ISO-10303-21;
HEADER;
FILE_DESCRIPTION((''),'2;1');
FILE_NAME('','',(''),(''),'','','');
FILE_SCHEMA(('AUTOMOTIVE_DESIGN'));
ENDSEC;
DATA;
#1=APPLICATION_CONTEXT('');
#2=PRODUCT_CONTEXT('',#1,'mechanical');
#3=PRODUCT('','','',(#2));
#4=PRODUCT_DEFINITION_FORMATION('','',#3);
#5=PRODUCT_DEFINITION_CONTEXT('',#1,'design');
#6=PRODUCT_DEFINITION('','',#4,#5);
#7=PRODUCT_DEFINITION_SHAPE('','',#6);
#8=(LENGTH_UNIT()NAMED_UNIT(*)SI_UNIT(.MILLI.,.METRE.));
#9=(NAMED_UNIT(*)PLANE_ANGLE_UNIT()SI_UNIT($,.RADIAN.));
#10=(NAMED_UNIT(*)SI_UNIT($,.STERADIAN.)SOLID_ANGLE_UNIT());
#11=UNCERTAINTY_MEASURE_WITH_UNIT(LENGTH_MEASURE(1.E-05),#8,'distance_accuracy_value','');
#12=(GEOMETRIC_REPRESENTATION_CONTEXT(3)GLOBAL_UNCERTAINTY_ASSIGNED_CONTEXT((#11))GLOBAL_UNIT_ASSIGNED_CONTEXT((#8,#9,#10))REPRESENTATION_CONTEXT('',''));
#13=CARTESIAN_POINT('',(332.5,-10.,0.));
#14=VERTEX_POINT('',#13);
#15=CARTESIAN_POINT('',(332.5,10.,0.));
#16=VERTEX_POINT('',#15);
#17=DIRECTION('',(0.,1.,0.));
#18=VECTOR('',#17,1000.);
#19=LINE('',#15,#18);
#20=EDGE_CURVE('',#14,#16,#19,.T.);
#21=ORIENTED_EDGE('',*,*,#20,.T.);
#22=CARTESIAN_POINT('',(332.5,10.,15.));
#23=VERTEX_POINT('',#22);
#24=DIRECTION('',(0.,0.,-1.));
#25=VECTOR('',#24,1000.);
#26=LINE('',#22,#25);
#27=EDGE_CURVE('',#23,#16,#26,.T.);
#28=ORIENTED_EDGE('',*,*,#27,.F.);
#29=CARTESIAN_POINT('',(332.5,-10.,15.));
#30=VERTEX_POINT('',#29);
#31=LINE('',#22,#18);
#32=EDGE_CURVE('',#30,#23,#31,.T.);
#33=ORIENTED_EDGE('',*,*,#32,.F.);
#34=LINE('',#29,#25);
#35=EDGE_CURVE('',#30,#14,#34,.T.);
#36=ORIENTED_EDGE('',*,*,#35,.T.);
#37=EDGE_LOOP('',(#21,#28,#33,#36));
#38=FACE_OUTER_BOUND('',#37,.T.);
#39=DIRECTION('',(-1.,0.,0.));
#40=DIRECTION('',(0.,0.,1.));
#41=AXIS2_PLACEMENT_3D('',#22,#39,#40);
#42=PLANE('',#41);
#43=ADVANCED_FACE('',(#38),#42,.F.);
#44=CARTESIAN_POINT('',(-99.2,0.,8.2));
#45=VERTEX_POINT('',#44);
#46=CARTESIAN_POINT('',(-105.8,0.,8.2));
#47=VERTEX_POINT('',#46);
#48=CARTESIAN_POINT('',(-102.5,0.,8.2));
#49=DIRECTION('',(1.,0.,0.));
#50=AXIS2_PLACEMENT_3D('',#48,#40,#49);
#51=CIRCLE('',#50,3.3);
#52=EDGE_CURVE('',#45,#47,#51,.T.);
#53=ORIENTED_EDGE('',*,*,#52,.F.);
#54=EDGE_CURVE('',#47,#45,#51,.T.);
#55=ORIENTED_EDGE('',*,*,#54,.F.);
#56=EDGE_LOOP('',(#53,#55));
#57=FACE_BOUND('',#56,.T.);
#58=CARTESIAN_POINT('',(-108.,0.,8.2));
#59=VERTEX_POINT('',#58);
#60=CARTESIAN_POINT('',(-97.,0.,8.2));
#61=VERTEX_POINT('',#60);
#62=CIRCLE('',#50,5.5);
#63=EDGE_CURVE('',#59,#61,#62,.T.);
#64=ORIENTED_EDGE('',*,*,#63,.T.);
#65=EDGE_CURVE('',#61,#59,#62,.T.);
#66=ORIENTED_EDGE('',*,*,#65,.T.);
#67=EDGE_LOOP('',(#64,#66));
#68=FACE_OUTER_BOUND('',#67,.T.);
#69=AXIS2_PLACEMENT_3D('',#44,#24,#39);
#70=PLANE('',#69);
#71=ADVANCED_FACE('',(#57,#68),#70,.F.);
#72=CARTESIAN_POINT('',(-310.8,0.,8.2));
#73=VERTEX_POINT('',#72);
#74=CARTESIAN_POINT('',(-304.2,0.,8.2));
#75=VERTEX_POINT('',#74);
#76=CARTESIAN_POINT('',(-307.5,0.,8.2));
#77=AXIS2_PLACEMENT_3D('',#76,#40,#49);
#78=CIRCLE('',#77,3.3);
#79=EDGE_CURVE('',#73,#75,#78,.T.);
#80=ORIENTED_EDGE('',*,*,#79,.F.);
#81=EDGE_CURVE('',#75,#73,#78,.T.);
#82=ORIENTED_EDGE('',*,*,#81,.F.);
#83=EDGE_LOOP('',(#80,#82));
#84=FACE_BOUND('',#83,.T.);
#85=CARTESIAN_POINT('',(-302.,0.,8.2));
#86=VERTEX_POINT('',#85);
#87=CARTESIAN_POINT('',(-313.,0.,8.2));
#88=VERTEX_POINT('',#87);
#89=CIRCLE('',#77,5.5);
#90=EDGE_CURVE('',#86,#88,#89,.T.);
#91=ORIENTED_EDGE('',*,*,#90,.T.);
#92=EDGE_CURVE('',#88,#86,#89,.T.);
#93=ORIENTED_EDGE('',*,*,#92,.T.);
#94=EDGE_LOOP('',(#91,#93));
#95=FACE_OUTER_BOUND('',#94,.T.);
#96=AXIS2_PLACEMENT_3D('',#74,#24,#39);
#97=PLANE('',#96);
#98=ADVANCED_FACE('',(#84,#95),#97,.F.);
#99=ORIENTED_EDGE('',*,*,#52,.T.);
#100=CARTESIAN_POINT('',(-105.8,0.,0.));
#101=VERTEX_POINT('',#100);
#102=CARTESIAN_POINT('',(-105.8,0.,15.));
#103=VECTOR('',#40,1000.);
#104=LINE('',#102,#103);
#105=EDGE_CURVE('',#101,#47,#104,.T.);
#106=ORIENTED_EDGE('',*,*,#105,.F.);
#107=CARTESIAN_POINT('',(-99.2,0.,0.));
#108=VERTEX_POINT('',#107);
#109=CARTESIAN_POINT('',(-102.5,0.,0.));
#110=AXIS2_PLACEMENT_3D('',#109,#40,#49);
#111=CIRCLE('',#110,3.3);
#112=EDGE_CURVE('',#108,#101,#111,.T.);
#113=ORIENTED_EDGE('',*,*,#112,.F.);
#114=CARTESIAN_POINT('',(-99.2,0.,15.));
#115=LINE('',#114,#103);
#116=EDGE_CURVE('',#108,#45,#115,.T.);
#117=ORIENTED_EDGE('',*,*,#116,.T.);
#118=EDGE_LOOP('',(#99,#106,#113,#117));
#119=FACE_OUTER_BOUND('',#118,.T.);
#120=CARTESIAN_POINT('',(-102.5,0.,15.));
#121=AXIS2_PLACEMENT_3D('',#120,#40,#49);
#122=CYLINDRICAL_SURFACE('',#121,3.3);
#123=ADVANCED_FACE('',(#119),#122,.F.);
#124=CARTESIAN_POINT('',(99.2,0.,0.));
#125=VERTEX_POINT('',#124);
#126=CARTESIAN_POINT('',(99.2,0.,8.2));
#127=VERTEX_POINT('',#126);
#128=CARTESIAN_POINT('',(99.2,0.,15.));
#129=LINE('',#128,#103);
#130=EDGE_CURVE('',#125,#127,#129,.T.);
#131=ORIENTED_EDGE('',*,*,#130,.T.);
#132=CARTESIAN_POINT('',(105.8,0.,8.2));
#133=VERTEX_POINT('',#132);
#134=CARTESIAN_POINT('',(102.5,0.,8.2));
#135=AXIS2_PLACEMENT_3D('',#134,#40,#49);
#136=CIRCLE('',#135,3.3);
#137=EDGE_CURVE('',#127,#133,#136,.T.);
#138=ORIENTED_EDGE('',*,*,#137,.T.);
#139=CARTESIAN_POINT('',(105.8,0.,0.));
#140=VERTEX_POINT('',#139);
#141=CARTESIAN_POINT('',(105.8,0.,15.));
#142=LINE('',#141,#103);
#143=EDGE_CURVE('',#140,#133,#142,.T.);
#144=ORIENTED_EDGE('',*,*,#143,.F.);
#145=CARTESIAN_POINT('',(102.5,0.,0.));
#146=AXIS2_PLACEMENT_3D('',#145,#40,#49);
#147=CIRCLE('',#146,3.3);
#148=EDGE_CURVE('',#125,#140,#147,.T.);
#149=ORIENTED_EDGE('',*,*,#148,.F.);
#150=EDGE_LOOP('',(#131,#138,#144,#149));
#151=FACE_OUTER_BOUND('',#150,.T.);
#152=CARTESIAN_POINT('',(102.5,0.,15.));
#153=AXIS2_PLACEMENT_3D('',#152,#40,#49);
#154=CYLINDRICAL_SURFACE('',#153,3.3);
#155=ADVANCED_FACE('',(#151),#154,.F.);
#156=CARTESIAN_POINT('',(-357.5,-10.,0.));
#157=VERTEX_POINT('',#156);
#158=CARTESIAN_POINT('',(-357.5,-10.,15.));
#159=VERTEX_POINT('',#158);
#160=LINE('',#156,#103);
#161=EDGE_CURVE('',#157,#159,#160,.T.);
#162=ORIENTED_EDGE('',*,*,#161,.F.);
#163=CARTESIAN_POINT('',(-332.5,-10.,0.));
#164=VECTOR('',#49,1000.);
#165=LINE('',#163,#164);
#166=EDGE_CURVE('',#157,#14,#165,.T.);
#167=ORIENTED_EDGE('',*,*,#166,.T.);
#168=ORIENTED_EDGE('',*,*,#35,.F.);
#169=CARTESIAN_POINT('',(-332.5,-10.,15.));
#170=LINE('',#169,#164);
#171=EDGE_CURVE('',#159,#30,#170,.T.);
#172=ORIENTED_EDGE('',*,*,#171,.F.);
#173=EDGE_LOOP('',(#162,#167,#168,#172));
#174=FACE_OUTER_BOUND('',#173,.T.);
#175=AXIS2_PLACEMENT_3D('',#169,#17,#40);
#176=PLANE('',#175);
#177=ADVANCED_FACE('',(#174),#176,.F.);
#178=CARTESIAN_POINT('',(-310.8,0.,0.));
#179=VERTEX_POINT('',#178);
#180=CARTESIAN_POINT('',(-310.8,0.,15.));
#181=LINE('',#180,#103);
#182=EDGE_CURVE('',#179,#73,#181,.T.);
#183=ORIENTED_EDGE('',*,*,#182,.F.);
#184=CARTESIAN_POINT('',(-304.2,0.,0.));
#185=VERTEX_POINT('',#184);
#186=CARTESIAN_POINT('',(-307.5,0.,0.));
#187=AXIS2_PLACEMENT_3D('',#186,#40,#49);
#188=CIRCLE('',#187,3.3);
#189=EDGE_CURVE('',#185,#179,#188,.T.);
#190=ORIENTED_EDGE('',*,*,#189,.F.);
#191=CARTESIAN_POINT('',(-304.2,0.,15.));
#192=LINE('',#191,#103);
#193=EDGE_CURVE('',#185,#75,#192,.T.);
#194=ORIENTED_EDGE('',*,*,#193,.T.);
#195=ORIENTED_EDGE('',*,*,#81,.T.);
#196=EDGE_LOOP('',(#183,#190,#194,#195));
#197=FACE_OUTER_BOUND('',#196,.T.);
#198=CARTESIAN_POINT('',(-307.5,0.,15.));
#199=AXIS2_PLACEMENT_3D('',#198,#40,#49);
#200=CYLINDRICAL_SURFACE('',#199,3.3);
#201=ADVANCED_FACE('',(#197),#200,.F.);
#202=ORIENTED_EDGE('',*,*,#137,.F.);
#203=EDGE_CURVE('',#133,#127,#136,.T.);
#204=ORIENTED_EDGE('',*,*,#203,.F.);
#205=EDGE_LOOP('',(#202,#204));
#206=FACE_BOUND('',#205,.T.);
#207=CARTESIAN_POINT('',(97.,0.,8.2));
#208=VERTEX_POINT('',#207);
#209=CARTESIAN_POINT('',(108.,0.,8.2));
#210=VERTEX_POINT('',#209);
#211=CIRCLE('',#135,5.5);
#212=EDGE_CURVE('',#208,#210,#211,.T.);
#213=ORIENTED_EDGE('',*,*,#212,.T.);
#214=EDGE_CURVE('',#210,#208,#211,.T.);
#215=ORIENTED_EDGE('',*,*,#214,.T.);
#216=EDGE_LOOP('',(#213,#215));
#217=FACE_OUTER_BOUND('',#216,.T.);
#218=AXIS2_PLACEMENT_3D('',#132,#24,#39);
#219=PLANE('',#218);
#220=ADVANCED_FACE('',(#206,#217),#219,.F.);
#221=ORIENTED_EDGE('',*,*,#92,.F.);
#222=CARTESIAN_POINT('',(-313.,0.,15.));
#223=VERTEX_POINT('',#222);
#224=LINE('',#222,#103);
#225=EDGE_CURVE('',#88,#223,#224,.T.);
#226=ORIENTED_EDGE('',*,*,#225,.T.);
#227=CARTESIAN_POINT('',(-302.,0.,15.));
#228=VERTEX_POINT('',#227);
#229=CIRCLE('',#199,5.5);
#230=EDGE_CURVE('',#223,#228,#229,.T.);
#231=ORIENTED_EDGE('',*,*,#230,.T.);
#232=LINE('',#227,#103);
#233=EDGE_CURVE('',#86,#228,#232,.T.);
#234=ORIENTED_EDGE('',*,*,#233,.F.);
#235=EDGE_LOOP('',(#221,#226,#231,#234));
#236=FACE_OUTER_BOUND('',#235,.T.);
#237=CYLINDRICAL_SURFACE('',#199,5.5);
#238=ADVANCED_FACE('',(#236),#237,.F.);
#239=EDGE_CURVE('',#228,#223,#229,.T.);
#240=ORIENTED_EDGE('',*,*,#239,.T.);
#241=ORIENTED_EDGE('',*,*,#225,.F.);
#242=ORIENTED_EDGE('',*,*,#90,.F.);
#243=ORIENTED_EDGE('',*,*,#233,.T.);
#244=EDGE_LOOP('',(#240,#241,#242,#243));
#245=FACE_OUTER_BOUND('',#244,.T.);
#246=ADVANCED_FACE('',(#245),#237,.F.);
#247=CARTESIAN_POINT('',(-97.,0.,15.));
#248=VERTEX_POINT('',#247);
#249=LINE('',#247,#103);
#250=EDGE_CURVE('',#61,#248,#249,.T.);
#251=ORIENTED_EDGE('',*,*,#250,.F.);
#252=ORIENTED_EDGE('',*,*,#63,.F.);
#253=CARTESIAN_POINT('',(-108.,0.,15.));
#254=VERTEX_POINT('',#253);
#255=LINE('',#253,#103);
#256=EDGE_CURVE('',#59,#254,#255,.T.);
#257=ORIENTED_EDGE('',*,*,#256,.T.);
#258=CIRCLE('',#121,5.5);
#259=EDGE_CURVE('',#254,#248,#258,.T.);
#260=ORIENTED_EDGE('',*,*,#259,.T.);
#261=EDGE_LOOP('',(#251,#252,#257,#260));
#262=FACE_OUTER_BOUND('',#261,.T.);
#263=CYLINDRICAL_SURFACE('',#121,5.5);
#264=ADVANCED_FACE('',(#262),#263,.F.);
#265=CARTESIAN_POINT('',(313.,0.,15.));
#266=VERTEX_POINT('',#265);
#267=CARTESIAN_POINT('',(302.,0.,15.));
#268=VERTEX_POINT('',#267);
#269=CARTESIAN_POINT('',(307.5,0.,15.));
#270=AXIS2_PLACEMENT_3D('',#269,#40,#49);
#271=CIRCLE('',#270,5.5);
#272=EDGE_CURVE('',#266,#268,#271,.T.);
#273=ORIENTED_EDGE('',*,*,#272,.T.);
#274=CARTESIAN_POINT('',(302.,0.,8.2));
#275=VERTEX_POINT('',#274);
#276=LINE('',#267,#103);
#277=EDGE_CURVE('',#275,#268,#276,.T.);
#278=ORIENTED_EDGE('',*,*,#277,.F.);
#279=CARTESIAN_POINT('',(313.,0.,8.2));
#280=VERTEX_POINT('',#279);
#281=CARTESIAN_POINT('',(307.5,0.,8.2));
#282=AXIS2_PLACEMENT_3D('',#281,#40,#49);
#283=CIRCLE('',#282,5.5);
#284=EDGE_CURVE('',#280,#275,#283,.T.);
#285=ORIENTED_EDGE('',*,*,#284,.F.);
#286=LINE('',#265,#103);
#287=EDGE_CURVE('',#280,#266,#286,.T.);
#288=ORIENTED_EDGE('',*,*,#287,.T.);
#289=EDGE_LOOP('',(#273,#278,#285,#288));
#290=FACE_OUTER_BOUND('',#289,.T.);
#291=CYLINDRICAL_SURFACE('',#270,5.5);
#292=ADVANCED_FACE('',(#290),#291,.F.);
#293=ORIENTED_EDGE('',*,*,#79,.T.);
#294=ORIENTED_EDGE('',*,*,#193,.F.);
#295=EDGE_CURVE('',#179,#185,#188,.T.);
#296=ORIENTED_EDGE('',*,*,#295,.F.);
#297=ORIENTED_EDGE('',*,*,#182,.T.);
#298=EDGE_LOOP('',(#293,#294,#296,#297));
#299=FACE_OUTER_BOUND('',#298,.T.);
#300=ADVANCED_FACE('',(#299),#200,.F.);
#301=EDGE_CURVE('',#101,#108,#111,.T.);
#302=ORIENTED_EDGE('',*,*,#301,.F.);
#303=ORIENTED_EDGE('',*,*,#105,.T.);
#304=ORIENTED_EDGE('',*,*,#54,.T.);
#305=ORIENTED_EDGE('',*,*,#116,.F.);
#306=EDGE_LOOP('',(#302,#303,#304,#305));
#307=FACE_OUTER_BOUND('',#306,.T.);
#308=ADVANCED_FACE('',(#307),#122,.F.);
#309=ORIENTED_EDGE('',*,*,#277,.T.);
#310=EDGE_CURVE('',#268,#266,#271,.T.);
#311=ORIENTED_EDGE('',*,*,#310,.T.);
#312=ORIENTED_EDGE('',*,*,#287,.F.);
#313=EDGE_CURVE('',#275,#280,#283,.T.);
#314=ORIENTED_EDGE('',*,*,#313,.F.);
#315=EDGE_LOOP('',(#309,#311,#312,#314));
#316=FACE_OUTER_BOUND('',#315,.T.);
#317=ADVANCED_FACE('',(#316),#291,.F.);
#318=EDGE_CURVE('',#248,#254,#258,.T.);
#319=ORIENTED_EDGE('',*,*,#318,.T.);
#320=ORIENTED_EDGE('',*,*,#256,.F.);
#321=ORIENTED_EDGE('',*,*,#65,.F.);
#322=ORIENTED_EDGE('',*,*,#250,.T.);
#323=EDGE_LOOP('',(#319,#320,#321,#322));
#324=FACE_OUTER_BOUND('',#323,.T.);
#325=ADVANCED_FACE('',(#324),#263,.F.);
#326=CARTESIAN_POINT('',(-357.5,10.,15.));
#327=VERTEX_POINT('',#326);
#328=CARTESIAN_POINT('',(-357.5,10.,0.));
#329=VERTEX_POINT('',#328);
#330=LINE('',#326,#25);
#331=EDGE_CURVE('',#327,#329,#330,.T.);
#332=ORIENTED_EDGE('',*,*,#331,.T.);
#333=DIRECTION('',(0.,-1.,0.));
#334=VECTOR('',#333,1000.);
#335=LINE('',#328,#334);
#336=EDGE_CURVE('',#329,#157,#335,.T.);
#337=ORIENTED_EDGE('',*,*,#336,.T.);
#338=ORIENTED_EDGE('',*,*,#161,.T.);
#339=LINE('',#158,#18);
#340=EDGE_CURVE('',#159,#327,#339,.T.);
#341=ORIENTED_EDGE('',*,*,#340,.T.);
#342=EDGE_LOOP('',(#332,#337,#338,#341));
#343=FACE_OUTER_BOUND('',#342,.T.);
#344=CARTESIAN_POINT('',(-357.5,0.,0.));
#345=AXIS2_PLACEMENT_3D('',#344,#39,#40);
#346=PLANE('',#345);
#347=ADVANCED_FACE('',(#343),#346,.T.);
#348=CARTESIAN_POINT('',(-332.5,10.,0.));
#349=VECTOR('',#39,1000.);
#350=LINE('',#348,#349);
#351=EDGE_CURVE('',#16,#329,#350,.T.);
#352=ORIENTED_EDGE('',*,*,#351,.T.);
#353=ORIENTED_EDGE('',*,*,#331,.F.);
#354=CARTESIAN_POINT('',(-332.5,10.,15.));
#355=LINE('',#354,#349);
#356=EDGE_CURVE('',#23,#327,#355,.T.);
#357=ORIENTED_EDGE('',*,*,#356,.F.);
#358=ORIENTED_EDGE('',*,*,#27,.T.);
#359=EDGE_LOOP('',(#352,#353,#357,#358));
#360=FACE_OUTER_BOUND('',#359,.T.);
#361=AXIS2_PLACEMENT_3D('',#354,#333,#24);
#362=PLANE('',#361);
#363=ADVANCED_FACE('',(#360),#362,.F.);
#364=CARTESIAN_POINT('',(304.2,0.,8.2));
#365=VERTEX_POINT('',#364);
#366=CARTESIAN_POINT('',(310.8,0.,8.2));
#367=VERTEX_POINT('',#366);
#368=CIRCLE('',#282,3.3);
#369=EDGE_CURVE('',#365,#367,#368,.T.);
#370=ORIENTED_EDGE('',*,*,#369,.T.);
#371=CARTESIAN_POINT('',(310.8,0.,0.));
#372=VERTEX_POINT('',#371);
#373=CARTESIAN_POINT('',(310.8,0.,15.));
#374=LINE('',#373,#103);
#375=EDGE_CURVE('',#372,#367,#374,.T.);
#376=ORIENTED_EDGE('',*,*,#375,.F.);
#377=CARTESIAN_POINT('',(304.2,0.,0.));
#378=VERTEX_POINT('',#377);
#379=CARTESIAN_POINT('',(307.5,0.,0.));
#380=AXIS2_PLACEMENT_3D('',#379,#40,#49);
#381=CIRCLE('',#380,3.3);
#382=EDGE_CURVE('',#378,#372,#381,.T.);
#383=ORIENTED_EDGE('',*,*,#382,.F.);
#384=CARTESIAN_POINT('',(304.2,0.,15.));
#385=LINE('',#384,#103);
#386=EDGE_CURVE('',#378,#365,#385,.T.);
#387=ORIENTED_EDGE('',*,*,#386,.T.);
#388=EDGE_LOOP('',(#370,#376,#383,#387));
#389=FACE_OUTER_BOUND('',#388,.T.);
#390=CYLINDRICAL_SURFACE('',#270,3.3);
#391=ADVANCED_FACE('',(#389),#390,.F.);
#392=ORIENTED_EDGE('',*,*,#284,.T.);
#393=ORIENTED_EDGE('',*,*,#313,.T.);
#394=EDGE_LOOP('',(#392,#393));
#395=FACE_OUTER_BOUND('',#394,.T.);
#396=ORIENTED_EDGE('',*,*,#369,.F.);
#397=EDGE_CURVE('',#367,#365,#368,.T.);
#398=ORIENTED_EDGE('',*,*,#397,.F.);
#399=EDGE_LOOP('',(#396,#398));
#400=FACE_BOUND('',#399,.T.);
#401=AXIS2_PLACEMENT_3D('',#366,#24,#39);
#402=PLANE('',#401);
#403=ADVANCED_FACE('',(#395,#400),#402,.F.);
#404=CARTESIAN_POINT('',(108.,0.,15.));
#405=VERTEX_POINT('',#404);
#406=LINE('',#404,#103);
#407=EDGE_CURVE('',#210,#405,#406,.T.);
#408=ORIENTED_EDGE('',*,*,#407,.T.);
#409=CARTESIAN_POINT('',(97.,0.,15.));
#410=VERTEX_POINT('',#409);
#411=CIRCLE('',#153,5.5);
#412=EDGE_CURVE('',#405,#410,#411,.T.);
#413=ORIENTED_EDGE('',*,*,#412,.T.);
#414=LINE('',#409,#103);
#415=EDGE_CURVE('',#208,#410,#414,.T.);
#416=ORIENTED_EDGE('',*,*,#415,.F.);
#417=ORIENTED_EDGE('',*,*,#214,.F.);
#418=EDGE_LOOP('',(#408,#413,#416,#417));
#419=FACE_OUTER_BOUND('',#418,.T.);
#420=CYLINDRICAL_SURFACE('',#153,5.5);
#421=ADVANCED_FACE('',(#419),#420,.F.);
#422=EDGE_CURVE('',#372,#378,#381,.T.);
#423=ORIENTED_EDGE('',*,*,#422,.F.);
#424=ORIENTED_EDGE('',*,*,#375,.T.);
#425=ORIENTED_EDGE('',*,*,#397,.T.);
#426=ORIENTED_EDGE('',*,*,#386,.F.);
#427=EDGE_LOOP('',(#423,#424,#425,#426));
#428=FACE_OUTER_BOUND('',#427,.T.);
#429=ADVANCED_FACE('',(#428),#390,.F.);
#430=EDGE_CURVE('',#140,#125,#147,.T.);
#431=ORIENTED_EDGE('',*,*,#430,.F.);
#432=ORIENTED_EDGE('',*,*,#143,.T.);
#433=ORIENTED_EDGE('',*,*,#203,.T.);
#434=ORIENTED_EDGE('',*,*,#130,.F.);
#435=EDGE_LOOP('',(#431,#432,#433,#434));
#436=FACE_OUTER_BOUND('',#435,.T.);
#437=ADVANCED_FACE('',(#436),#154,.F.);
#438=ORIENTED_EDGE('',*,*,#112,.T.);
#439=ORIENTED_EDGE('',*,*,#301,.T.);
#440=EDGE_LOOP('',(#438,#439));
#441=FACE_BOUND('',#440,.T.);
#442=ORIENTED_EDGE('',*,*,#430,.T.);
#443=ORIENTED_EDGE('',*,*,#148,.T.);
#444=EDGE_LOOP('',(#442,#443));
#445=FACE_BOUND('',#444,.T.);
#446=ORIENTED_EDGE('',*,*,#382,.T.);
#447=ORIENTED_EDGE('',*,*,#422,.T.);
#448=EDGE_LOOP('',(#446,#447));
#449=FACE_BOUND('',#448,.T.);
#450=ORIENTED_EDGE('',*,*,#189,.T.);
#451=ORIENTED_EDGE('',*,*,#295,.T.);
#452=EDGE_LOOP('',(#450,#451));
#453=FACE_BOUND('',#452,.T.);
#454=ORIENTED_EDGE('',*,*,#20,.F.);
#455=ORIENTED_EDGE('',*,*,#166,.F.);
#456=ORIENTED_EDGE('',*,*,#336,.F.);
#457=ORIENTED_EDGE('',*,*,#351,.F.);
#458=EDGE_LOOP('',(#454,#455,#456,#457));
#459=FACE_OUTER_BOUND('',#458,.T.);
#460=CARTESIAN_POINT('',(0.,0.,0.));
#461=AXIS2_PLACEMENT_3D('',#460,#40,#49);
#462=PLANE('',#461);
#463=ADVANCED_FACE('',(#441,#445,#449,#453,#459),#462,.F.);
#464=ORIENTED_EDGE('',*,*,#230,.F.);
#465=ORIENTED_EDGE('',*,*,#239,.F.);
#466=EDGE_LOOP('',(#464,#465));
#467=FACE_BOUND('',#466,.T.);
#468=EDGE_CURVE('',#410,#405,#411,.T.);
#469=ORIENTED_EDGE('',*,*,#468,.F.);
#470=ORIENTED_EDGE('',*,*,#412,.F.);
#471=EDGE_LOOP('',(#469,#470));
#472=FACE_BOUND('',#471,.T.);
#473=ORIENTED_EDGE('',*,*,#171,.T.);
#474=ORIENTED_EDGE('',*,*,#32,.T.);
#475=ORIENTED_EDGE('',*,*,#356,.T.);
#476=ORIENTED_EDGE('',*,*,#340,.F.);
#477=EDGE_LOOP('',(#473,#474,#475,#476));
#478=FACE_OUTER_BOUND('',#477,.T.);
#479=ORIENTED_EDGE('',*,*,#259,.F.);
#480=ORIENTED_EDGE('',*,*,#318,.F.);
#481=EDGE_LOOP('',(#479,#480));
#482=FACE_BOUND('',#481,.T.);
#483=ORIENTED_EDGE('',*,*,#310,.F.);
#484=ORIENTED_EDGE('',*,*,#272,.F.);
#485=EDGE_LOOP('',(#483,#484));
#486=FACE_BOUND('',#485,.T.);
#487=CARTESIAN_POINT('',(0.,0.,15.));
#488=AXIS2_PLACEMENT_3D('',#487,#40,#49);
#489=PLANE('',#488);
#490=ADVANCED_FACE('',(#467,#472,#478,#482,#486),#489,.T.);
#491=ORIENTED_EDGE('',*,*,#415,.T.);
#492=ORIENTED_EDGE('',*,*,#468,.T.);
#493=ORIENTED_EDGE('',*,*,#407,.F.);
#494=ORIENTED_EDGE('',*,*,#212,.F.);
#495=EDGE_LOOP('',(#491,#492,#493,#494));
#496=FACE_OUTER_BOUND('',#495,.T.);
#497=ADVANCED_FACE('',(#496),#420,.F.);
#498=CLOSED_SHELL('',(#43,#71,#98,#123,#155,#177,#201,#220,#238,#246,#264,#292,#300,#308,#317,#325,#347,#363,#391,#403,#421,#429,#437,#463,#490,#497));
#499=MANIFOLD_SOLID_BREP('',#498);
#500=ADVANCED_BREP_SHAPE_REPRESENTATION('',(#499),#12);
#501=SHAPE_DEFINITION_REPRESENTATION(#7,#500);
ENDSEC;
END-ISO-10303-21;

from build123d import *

# Parameters (mm, degrees)
SKETCH_1_W                = 665
SKETCH_1_H                = 20
EXTRUDE_1_DEPTH           = 15
HOLE_WIZARD_1_D           = 6.6
HOLE_WIZARD_1_CBORE_D     = 11
HOLE_WIZARD_1_CBORE_DEPTH = 6.8
SKETCH_5_W                = 15
SKETCH_5_H                = 20
EXTRUDE_2_DEPTH           = 25


with BuildPart() as part:
    # 草图1 → 凸台-拉伸1 (new body)
    with BuildSketch(Plane.XY):
        Rectangle(SKETCH_1_W, SKETCH_1_H)
    extrude(amount=EXTRUDE_1_DEPTH)

    # 打孔尺寸(%根据)内六角圆柱头螺钉的类型1 (through all)
    with Locations(Plane.XY.offset(15)):
        with Locations((102.5, 0), (-307.5, 0), (307.5, 0), (-102.5, 0)):
            CounterBoreHole(HOLE_WIZARD_1_D / 2, HOLE_WIZARD_1_CBORE_D / 2, HOLE_WIZARD_1_CBORE_DEPTH)

    # 草图5 → 凸台-拉伸2 (add)
    with BuildSketch(Plane.ZY.offset(332.5)):
        with Locations((7.5, 0)):
            Rectangle(SKETCH_5_W, SKETCH_5_H)
    extrude(amount=EXTRUDE_2_DEPTH)


solid = part.part
